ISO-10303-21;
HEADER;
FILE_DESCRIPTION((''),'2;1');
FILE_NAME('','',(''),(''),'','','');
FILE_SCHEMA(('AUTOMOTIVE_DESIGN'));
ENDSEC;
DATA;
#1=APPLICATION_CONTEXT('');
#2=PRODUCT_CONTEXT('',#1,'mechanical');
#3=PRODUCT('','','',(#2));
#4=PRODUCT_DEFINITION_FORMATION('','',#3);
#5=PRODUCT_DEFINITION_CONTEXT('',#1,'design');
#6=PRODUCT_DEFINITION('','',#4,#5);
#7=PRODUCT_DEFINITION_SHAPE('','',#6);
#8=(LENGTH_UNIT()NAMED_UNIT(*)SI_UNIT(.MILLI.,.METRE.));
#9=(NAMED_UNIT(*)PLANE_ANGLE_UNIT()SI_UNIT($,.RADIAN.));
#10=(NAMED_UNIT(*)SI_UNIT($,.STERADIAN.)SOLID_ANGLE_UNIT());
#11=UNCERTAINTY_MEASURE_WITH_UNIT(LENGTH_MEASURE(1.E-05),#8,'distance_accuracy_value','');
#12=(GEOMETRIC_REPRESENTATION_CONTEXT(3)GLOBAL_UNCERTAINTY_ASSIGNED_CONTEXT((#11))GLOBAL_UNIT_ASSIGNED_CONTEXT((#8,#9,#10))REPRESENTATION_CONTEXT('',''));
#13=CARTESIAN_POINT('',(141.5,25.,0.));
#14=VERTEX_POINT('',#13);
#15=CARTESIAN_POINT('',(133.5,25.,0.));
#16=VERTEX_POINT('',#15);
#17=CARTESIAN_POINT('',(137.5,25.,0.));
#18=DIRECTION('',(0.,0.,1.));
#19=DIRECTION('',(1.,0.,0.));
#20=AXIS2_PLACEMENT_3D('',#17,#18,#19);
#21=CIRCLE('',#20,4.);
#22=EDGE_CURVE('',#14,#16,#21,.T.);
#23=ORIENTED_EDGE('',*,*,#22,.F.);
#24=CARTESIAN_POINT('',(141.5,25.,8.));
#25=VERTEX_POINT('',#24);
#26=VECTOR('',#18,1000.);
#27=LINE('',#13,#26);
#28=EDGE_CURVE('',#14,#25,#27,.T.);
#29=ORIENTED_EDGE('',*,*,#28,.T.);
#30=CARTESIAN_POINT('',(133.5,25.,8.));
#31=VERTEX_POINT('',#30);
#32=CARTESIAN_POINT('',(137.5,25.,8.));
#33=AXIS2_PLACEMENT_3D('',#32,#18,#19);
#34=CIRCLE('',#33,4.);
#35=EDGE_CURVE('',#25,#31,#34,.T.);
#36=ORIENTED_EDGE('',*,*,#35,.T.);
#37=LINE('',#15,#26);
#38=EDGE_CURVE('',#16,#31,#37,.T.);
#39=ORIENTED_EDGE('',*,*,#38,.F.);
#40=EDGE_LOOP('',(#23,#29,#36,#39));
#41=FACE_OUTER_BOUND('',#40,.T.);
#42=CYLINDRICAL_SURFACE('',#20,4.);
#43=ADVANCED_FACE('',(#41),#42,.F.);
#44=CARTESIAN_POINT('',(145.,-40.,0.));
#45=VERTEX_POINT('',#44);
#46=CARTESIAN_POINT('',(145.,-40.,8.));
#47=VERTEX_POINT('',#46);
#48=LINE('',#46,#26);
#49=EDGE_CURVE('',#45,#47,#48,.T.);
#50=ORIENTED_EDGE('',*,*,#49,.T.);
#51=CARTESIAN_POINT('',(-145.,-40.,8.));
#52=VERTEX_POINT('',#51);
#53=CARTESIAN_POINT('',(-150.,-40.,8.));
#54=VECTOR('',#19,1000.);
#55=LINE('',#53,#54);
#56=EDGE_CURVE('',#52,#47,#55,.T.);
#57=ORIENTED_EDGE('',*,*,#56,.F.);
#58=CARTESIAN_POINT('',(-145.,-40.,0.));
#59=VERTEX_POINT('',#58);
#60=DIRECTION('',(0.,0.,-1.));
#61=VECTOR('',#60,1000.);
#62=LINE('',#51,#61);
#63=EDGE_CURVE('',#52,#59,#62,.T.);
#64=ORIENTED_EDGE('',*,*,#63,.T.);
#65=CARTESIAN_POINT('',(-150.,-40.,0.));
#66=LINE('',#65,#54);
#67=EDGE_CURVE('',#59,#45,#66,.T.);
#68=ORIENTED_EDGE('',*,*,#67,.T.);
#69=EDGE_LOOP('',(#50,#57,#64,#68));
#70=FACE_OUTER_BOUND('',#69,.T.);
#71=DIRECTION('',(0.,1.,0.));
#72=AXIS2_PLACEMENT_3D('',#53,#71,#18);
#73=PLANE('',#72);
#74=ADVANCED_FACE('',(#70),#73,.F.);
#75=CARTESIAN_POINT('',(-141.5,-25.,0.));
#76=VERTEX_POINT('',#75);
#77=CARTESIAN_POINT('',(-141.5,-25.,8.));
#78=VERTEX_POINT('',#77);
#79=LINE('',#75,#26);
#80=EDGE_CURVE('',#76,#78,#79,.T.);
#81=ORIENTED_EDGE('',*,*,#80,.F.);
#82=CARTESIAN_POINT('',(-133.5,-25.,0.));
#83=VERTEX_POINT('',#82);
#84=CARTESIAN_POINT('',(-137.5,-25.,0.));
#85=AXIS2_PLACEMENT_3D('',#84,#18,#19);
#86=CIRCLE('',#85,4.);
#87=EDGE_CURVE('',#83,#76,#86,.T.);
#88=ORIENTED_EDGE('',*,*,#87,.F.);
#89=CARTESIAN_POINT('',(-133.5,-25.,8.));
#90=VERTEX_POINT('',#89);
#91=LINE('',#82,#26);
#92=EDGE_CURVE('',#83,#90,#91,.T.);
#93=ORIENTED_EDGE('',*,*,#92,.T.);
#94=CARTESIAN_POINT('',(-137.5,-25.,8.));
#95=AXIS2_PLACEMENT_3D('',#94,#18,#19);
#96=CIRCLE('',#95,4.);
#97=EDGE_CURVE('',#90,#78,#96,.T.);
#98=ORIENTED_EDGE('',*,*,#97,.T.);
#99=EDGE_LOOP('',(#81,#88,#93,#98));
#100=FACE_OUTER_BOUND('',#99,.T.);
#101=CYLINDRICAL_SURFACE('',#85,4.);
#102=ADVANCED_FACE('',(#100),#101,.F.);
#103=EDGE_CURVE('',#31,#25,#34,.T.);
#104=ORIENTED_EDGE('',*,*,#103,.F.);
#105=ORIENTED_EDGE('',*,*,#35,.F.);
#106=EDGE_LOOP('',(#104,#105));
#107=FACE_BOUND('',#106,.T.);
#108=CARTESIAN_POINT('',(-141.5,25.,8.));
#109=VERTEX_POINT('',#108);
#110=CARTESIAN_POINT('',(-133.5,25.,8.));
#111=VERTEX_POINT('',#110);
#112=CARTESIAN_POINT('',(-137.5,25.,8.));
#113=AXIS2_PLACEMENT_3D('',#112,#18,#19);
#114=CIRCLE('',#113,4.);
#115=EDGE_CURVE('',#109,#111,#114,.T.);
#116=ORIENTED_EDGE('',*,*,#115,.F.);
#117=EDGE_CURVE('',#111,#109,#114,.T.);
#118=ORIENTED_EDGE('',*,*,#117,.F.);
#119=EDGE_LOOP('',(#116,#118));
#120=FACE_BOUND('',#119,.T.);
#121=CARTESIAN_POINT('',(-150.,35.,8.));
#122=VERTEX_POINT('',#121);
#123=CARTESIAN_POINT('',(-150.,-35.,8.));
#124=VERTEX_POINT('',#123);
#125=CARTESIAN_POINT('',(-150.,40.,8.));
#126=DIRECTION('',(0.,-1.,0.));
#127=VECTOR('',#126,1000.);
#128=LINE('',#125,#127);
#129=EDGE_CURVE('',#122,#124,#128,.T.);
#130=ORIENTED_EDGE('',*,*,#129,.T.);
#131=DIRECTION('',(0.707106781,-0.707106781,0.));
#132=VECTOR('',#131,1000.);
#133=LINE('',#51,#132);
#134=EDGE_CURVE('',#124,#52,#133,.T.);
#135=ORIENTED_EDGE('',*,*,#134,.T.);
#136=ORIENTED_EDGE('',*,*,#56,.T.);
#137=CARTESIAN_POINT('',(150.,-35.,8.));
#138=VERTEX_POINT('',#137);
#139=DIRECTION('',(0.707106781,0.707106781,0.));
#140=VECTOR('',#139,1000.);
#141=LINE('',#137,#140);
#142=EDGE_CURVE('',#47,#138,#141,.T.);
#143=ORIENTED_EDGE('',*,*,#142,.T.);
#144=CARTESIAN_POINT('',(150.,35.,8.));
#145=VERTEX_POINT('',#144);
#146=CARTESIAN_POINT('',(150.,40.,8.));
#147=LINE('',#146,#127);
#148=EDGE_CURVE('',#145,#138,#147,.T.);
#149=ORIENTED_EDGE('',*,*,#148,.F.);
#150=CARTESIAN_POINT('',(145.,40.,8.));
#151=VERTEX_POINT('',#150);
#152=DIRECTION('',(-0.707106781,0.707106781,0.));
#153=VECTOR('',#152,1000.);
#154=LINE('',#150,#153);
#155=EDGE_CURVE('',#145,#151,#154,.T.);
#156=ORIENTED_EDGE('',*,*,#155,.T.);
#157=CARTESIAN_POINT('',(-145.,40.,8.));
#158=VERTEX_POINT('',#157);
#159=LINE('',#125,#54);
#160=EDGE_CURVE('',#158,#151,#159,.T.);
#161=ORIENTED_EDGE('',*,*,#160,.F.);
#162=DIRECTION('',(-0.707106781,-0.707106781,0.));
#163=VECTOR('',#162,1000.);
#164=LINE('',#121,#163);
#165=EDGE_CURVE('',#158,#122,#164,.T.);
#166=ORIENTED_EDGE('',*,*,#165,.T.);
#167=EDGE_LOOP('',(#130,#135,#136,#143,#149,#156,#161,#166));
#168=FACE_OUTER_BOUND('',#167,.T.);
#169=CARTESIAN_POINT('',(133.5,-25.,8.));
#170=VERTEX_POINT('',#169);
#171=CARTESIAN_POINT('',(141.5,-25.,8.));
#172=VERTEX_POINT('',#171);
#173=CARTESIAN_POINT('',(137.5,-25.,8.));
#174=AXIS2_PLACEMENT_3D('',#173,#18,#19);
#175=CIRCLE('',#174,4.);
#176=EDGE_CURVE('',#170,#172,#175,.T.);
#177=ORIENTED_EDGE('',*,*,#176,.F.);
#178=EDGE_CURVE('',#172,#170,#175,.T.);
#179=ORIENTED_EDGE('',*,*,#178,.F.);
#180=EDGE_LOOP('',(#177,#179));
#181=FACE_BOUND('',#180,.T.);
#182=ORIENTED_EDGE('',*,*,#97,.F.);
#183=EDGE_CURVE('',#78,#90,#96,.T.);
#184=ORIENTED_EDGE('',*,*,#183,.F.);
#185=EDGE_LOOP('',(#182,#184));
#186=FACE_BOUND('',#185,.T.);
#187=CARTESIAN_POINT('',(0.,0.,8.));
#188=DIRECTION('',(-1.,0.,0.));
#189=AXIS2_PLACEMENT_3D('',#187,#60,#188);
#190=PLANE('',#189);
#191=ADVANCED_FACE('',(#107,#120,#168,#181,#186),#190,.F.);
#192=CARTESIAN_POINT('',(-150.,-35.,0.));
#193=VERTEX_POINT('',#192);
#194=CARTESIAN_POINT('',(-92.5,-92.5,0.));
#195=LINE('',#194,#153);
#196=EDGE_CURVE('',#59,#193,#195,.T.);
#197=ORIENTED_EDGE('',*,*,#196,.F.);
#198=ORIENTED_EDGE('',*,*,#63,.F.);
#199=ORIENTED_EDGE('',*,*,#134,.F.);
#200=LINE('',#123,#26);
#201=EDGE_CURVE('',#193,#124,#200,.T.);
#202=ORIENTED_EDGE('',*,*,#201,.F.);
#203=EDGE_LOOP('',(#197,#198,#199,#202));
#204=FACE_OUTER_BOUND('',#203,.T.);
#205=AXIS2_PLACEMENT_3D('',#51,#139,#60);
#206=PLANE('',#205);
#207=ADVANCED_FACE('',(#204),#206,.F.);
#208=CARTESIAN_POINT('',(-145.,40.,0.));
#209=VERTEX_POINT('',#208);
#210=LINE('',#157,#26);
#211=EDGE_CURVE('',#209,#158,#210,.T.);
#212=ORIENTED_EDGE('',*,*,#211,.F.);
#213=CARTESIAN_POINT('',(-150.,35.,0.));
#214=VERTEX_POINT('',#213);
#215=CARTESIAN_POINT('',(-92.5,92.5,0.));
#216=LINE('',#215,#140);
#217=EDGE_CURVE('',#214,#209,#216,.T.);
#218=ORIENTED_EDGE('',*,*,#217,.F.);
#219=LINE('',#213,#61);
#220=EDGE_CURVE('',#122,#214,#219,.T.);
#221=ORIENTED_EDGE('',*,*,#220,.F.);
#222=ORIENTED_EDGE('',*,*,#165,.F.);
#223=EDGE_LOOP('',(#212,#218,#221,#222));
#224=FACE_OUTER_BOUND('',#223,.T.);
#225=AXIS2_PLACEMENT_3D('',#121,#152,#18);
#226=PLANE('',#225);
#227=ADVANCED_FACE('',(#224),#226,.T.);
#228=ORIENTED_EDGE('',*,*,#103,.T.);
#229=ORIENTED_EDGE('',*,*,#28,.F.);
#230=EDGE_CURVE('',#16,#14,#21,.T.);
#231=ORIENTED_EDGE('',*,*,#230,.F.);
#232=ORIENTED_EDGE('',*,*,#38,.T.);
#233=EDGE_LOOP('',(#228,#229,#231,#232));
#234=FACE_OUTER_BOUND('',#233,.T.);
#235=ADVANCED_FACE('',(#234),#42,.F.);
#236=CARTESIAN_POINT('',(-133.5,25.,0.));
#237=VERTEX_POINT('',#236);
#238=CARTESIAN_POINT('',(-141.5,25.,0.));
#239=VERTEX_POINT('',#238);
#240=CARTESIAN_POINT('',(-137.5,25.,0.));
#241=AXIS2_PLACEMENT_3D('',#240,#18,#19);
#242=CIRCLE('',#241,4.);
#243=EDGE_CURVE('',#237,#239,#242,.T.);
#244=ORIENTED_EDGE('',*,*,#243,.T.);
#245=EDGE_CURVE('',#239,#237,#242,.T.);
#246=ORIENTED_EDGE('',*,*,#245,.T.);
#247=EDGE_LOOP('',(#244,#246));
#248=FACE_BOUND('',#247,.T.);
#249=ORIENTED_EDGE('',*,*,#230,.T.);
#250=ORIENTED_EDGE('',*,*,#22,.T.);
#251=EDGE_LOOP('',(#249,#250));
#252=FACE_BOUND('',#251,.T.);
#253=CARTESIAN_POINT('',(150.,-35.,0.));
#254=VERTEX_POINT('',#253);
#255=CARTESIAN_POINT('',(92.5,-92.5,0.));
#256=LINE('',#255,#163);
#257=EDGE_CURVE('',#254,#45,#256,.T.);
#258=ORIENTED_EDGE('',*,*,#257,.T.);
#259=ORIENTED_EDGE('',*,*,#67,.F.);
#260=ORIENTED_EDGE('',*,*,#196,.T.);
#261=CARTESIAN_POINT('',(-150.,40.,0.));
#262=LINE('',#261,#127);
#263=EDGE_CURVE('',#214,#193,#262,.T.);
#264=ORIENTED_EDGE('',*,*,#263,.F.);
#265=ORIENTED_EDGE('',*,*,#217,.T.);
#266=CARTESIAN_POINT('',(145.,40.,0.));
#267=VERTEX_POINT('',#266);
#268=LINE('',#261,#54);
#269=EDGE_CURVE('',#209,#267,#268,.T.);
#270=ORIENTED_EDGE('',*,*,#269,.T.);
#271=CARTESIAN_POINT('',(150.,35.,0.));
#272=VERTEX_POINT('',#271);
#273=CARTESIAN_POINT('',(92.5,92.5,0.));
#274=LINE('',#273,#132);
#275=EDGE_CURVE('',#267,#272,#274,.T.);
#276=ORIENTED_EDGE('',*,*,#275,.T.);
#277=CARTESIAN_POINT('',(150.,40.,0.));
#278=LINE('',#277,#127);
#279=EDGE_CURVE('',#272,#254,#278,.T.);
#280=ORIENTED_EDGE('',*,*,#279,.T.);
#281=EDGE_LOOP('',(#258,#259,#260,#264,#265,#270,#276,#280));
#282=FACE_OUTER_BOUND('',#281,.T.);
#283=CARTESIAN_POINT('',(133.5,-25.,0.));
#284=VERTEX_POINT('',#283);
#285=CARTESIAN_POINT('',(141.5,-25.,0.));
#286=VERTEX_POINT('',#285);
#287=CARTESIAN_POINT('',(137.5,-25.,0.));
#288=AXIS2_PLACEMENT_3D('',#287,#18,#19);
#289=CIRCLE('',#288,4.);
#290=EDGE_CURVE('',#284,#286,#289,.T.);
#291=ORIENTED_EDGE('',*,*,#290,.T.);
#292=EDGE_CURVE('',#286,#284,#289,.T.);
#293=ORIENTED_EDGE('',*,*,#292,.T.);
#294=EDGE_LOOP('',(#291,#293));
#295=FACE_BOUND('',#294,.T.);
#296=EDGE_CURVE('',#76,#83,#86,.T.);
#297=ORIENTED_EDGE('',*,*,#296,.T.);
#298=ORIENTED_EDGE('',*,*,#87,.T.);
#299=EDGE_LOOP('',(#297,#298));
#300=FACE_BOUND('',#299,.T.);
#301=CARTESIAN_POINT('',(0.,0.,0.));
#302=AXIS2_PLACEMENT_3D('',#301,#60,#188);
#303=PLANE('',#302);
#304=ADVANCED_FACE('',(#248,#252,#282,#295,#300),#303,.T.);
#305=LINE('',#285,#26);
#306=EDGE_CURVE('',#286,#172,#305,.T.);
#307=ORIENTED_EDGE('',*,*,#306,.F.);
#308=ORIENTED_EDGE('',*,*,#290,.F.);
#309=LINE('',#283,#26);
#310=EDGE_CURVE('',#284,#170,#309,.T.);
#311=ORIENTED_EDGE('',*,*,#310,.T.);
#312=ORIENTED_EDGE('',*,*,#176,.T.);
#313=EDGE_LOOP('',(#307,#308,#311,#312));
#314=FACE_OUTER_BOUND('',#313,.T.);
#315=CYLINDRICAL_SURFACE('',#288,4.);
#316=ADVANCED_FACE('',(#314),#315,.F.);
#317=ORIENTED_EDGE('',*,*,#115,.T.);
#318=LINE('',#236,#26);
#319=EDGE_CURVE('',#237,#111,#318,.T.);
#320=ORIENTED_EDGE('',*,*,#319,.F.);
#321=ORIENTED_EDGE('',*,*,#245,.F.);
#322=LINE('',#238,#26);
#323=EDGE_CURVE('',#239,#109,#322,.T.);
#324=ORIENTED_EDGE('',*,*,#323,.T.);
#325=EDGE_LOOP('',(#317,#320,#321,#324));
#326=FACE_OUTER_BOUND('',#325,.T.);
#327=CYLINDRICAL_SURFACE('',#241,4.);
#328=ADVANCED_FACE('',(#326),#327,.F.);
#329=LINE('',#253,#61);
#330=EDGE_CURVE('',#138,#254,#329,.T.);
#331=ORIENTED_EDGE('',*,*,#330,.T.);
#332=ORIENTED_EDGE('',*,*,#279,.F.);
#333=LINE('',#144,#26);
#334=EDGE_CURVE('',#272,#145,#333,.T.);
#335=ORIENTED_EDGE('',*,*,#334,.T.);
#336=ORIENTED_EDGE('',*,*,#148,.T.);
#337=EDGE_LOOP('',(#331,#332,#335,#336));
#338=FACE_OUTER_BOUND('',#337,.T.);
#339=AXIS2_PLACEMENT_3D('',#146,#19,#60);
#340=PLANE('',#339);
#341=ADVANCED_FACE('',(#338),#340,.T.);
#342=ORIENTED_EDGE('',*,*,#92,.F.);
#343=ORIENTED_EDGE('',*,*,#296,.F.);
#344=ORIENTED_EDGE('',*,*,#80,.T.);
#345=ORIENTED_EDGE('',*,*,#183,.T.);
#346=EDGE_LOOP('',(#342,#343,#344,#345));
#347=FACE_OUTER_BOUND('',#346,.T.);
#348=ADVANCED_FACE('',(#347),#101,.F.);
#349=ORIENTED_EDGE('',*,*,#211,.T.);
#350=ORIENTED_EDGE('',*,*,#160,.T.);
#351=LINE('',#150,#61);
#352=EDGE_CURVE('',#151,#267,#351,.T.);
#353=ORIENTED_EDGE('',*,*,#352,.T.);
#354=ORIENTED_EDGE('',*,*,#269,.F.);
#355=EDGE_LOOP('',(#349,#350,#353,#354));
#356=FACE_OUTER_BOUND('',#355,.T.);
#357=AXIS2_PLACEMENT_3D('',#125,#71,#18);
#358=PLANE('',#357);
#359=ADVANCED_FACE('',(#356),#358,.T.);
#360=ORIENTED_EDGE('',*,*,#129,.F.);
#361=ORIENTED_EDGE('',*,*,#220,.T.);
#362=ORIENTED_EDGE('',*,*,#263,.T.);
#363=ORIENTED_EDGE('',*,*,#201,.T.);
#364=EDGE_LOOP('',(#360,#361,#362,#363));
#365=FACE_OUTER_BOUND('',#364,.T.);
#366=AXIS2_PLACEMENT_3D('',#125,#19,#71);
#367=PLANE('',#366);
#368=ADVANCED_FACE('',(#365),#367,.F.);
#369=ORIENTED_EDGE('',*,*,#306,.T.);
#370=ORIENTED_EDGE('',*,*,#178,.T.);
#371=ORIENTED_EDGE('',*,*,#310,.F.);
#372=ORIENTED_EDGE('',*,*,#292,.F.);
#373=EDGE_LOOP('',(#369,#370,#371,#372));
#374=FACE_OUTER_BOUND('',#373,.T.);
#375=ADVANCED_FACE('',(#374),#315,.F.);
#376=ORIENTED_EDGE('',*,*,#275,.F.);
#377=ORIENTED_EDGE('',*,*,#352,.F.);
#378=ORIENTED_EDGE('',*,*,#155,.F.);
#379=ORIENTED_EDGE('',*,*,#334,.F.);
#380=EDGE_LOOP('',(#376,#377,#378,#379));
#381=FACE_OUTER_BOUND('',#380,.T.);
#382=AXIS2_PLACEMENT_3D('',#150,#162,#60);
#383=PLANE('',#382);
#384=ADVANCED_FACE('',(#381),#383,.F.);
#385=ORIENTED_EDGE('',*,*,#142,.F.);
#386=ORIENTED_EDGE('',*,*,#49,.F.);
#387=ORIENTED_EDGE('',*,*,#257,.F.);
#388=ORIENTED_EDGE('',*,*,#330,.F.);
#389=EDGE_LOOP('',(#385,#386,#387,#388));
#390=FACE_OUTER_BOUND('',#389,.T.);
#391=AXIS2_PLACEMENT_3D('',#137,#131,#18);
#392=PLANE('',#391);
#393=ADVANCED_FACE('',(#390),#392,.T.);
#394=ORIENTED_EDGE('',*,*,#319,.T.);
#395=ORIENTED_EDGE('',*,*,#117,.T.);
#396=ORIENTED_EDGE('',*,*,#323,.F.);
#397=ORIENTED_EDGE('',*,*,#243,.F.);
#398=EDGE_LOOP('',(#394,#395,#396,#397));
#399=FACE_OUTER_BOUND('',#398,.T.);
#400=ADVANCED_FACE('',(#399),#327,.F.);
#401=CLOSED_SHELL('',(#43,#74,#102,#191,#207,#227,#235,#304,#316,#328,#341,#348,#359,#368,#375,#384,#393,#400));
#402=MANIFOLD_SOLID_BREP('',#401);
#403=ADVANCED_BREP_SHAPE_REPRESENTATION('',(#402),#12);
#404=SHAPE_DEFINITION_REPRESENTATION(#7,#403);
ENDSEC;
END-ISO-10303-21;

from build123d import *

# Parameters (mm, degrees)
SKETCH1_W           = 300
SKETCH1_H           = 80
BOSS_EXTRUDE1_DEPTH = 8
SKETCH2_R           = 4
CUT_EXTRUDE1_DEPTH  = 8
CHAMFER1_SIZE       = 5


with BuildPart() as part:
    # Sketch1 → Boss-Extrude1 (new body)
    with BuildSketch(Plane.XY):
        Rectangle(SKETCH1_W, SKETCH1_H)
    extrude(amount=BOSS_EXTRUDE1_DEPTH)

    # Sketch2 → Cut-Extrude1 (cut)
    with BuildSketch(Plane.XY.offset(8)):
        with Locations((-137.5, 25)):
            Circle(SKETCH2_R)
        with Locations((-137.5, -25)):
            Circle(SKETCH2_R)
        with Locations((137.5, 25)):
            Circle(SKETCH2_R)
        with Locations((137.5, -25)):
            Circle(SKETCH2_R)
    extrude(amount=-CUT_EXTRUDE1_DEPTH, mode=Mode.SUBTRACT)

    # Chamfer1
    chamfer1_edges = [part.edges().sort_by_distance(p)[0] for p in [
        (-150, -40, 4),
        (-150, 40, 4),
        (150, 40, 4),
        (150, -40, 4),
    ]]
    chamfer(chamfer1_edges, length=CHAMFER1_SIZE)


solid = part.part
